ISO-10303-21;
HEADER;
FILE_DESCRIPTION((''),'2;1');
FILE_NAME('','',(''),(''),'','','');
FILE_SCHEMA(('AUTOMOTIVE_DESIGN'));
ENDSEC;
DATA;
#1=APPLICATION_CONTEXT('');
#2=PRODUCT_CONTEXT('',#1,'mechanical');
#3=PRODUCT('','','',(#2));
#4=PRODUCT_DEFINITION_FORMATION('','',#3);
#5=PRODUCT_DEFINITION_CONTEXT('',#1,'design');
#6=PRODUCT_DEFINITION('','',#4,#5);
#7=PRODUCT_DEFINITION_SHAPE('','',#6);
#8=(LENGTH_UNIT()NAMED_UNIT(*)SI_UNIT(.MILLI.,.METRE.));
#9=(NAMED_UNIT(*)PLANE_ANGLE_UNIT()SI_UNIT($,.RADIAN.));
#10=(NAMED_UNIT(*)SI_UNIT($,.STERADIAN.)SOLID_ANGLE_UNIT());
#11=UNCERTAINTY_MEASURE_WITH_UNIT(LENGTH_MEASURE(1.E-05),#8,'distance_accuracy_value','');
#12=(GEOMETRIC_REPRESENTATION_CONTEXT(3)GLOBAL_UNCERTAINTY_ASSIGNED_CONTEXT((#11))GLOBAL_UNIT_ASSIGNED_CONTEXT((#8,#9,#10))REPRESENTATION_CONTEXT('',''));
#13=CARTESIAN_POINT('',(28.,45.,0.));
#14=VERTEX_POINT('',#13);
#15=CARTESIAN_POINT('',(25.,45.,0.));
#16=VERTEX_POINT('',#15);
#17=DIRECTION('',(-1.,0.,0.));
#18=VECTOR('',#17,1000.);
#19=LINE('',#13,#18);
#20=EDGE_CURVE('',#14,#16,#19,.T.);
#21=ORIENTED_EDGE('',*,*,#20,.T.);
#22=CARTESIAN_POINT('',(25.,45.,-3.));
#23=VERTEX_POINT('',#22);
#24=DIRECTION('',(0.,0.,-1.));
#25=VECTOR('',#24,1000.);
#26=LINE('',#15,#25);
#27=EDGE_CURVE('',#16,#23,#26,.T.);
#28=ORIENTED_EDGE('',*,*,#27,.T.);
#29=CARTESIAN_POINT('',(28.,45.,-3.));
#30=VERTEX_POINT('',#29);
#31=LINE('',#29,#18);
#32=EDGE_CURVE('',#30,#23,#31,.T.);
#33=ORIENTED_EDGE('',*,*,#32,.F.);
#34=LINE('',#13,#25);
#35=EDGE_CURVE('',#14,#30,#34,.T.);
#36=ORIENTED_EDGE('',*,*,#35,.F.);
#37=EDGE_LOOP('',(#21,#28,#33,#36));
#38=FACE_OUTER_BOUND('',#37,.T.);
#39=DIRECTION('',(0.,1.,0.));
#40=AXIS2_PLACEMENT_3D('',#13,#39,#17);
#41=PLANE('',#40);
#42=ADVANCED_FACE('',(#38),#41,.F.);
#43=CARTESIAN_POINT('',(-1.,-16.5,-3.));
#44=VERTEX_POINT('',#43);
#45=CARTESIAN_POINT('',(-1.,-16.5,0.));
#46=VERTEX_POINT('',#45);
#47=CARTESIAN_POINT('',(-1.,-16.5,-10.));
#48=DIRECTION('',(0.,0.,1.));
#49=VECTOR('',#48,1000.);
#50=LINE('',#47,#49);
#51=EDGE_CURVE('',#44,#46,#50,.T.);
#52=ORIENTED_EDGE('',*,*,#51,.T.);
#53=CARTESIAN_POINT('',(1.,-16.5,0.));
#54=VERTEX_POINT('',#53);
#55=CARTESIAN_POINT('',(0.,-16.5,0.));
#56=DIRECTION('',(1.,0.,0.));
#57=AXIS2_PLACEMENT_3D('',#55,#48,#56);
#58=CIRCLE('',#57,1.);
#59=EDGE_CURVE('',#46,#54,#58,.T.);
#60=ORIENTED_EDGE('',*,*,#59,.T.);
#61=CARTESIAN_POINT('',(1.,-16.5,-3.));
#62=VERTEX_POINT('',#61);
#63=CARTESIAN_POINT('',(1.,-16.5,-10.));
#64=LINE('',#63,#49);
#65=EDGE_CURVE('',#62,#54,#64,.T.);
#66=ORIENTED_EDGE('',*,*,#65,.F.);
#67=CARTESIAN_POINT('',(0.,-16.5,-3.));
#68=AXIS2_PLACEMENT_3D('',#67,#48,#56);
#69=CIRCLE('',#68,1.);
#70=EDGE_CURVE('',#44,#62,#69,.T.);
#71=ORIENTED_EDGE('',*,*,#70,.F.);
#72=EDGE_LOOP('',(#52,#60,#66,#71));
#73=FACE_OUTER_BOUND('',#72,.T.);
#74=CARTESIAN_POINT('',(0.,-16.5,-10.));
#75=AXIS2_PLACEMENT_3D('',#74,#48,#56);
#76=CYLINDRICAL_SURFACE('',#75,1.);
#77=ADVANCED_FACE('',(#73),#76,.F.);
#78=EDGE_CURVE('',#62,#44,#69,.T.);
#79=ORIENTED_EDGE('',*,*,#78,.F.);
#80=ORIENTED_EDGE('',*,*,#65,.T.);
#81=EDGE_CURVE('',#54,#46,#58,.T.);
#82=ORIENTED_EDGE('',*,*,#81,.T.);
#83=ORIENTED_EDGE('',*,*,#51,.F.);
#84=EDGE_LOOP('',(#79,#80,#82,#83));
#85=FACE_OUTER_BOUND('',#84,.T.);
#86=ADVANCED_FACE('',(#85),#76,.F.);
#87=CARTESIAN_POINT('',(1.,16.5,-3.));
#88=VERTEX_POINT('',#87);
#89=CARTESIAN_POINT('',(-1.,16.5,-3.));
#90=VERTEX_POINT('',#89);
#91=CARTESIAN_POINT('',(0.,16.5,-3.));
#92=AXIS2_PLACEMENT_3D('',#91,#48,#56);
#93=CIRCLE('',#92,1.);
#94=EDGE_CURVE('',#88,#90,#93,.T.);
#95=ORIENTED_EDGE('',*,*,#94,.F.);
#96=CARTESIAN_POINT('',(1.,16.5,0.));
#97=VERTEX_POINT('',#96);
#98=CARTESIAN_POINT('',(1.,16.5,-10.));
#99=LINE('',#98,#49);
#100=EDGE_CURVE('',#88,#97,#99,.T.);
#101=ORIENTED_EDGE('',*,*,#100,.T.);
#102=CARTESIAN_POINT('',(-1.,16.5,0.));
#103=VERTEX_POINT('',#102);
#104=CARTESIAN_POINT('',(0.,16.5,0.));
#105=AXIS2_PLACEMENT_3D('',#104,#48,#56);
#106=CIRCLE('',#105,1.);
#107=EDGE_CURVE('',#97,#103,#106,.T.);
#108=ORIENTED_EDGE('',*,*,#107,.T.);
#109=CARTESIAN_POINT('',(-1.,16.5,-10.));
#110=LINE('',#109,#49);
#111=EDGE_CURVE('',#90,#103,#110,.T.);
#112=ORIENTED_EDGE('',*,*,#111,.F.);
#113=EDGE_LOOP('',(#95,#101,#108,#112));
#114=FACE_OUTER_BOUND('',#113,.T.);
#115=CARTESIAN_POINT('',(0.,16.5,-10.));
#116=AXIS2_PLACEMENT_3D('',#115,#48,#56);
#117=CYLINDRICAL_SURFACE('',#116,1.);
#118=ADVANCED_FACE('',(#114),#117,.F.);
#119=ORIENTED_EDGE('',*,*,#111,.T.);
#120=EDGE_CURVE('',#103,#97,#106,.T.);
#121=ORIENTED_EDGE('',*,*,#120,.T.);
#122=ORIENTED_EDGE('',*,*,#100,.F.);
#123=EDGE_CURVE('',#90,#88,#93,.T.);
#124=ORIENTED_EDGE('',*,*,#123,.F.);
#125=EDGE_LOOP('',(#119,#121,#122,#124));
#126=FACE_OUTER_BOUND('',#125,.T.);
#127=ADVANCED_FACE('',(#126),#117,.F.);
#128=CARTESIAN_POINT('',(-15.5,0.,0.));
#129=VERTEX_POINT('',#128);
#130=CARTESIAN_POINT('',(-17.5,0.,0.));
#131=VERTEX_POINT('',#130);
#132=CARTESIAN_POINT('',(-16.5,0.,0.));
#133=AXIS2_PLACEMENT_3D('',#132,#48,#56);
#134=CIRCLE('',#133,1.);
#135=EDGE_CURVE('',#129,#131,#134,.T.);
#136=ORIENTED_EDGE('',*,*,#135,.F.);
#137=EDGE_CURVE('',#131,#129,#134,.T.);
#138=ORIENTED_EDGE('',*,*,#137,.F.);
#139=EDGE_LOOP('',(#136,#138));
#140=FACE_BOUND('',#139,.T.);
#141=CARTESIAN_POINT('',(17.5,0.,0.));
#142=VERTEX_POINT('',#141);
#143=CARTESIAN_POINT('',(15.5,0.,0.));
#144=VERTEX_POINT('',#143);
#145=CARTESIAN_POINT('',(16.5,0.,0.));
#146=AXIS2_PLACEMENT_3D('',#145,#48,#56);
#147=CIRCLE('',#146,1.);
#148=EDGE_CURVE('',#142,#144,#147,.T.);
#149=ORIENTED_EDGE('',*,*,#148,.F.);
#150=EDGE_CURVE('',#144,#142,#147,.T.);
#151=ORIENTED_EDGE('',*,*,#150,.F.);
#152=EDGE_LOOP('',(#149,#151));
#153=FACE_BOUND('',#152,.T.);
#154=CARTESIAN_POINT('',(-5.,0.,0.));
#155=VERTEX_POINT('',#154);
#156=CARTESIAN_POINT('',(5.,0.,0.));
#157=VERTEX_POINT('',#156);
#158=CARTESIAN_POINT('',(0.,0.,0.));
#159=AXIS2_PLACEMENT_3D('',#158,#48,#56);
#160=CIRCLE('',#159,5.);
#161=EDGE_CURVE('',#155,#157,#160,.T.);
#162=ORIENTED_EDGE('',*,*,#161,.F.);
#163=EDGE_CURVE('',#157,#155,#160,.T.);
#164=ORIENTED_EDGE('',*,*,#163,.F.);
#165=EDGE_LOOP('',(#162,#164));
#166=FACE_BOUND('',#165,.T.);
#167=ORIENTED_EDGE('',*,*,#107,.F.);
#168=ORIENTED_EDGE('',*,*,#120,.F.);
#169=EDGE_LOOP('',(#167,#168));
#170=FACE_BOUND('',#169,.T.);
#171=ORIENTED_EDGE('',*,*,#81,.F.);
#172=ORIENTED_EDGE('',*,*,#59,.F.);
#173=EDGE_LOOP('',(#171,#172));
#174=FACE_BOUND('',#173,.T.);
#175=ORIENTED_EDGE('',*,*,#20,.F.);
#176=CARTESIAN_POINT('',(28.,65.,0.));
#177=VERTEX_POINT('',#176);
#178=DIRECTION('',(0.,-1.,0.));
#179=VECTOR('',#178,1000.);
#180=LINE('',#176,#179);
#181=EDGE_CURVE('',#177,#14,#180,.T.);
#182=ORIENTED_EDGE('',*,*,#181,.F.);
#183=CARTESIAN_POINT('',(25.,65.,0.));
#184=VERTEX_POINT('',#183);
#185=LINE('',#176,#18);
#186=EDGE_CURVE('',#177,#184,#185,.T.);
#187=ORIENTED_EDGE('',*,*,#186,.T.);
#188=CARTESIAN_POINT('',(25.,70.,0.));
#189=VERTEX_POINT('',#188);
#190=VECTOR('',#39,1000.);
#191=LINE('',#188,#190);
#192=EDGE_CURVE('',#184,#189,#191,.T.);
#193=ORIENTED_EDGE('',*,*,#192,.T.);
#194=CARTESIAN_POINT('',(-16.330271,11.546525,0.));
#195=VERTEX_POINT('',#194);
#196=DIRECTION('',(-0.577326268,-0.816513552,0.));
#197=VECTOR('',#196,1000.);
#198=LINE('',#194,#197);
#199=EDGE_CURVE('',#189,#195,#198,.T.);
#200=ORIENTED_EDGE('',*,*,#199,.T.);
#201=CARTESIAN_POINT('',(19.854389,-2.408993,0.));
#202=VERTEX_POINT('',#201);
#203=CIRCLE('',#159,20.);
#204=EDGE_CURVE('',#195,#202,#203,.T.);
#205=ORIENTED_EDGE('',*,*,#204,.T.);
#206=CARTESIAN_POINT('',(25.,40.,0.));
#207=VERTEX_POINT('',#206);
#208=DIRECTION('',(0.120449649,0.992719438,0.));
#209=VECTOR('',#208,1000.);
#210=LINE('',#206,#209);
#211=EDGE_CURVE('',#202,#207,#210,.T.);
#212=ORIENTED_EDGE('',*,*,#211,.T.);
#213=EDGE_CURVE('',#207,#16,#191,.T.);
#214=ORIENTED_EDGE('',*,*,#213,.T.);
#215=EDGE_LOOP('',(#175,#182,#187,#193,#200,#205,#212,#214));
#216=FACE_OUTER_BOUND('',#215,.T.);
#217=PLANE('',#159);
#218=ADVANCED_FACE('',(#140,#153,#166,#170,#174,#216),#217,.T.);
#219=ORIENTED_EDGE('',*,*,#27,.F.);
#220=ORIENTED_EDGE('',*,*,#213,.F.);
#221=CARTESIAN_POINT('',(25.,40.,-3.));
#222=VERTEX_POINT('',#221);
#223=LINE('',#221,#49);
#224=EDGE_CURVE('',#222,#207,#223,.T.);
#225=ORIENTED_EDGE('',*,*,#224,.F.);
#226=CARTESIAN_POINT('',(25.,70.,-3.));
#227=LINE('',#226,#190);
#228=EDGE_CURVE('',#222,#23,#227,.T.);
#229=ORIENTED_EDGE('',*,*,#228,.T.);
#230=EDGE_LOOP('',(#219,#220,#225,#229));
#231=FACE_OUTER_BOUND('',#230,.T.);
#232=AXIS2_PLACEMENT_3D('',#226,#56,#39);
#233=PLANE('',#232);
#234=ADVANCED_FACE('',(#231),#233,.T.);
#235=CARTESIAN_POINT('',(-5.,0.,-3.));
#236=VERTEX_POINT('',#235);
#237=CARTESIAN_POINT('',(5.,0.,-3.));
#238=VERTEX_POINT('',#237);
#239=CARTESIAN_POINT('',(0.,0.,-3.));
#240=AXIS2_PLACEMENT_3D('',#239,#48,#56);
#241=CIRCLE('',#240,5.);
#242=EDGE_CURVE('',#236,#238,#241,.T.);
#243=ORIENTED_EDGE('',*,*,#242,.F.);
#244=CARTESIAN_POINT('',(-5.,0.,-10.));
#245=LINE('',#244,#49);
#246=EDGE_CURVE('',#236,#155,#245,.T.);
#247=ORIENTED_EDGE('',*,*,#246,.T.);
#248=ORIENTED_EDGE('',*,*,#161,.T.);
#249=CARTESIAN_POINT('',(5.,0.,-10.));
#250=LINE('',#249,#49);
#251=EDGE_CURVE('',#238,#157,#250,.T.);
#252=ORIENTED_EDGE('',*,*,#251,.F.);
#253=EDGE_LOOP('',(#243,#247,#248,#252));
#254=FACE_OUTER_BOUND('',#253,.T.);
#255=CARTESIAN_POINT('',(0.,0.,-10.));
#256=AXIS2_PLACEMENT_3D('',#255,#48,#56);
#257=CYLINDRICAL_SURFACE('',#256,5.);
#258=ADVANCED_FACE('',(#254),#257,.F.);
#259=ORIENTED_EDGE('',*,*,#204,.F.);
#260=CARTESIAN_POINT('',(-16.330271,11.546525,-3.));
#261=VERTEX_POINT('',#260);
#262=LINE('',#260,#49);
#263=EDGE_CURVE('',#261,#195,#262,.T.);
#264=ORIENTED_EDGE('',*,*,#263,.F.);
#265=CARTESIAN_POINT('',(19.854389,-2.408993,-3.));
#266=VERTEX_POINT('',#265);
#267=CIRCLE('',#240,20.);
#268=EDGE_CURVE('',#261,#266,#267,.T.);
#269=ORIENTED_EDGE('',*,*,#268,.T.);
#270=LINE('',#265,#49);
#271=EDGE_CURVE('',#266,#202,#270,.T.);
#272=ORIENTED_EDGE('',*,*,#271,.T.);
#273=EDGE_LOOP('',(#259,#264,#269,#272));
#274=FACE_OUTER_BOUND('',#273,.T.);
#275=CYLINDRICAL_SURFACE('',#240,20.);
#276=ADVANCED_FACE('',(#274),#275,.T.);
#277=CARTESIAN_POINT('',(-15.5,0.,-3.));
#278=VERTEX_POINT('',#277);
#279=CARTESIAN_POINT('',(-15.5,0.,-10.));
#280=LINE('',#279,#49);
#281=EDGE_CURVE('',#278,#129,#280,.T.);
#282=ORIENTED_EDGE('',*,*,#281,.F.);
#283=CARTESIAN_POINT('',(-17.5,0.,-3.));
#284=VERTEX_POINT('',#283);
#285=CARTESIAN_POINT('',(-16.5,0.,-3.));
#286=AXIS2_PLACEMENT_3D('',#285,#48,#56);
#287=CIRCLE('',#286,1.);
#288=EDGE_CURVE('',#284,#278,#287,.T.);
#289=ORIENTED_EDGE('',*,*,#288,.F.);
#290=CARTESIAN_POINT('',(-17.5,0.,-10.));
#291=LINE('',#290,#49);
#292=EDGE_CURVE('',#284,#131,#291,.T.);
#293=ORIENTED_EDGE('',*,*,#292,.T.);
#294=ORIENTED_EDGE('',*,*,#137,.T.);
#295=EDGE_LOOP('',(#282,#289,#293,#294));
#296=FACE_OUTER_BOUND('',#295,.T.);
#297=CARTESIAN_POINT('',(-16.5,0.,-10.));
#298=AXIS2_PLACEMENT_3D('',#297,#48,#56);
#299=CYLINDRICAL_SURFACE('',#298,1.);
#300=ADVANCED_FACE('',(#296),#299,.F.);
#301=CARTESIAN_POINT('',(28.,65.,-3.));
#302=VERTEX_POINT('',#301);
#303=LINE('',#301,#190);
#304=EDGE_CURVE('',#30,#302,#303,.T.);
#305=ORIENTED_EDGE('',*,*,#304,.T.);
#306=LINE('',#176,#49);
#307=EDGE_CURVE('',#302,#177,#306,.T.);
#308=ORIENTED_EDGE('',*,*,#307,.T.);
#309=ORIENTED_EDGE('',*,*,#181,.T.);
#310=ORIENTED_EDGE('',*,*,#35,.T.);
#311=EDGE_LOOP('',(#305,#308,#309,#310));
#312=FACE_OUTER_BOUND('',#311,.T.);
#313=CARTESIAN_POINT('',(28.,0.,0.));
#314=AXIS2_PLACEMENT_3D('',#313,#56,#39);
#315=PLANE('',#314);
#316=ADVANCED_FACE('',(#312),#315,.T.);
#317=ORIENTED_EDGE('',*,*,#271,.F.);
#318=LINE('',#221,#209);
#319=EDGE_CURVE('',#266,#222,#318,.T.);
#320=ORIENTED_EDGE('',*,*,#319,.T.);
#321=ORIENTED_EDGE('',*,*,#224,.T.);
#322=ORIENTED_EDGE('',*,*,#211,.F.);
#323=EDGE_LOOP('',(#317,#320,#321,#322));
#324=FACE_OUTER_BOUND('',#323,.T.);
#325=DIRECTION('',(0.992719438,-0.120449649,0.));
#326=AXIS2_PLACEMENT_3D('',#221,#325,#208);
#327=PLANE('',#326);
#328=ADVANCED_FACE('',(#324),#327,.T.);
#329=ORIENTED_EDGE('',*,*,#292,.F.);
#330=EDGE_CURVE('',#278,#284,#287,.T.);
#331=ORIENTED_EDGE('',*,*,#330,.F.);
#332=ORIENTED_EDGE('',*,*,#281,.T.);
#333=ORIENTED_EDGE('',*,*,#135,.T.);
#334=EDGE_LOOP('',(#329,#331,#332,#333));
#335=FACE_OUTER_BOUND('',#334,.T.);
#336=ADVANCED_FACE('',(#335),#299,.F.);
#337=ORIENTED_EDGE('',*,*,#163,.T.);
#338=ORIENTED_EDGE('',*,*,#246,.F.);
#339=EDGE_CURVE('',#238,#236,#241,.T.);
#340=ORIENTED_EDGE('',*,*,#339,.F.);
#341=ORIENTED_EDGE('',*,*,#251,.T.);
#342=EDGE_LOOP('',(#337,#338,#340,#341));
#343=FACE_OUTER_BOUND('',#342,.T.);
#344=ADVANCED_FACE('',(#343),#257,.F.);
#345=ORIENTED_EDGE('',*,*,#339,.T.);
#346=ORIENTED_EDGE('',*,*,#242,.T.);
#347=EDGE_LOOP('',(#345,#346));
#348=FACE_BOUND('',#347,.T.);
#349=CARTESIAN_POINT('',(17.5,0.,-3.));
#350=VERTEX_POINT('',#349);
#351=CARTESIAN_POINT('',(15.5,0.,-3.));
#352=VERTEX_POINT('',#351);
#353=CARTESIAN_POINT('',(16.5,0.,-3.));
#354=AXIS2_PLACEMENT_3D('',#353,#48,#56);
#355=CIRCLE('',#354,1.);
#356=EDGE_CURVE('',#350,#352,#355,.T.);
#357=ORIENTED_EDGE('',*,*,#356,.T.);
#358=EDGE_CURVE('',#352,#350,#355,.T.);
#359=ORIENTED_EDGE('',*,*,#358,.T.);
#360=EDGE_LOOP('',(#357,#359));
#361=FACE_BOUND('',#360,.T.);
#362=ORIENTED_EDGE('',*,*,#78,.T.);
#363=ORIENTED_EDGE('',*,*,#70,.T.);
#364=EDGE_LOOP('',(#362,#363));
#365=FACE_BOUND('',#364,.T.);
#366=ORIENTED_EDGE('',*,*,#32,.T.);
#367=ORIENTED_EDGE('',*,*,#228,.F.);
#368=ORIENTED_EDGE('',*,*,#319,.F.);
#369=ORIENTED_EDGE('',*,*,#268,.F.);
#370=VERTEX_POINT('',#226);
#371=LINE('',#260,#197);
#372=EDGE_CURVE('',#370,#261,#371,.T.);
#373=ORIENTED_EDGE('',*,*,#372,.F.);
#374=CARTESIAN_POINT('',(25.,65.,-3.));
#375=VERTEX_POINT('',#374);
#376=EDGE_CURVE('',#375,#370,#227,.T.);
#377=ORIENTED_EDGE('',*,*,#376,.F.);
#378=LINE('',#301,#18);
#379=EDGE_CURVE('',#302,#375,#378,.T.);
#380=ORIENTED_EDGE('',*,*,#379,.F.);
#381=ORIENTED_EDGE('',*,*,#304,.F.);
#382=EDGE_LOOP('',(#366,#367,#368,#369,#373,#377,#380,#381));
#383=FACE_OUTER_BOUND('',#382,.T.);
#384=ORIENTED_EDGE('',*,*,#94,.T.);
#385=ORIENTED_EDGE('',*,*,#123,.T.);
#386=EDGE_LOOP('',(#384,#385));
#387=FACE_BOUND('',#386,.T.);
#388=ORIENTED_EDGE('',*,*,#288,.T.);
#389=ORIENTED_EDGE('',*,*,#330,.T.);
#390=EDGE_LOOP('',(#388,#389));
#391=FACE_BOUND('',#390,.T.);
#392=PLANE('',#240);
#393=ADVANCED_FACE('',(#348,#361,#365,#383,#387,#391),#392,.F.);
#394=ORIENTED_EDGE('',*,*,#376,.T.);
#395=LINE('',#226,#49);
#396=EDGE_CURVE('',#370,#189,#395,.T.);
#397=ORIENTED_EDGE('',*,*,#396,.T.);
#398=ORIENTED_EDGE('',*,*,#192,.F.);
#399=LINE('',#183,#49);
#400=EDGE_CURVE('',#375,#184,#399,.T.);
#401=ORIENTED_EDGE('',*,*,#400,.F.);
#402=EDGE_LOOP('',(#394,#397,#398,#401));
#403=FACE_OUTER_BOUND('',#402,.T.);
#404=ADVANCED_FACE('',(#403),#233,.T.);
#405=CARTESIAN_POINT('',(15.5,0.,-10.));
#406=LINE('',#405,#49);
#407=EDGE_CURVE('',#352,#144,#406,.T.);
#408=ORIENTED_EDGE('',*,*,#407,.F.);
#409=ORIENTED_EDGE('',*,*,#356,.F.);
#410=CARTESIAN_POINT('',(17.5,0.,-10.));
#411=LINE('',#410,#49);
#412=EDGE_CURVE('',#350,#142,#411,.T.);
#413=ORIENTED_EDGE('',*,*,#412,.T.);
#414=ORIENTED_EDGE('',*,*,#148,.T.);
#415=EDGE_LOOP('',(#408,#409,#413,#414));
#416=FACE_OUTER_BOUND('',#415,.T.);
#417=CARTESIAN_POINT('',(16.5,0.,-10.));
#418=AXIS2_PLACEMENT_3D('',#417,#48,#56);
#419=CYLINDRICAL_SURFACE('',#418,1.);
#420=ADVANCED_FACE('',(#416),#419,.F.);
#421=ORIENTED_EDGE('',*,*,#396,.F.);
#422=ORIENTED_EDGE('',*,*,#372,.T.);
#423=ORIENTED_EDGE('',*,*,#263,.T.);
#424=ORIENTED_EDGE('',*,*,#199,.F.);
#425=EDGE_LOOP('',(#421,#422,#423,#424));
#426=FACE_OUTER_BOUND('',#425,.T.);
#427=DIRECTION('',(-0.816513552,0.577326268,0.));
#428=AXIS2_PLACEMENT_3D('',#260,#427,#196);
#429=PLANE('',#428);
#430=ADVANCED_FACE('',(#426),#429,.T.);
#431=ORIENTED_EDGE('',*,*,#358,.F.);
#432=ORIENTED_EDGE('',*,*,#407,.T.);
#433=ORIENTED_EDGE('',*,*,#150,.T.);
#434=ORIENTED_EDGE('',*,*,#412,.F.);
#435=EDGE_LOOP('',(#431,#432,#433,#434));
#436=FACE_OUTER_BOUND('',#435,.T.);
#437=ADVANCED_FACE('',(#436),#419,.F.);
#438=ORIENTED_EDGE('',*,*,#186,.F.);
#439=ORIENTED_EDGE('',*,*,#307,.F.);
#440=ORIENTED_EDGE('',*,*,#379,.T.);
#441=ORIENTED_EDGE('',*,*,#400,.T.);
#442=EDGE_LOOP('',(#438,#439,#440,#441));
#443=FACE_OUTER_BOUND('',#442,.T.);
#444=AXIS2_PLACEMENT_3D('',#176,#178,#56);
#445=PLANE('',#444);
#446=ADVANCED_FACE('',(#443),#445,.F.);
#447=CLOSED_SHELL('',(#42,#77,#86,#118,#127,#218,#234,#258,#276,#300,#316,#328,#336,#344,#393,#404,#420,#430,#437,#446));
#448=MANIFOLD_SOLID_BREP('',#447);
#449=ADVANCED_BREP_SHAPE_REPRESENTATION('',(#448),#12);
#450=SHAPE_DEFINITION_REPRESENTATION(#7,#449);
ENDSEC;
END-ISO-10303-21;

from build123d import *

# Parameters (mm, degrees)
BOSS_EXTRUDE1_DEPTH = 3
SKETCH2_R           = 5
CUT_EXTRUDE1_DEPTH  = 10
SKETCH4_W           = 3
SKETCH4_H           = 20
BOSS_EXTRUDE3_DEPTH = 3
SKETCH5_R           = 1
CUT_EXTRUDE2_DEPTH  = 10


with BuildPart() as part:
    # Sketch1 → Boss-Extrude1 (new body)
    with BuildSketch(Plane.XY):
        with BuildLine():
            Line((-16.33027103, 11.546525368), (25, 70))
            Line((25, 70), (25, 40))
            Line((25, 40), (19.854388756, -2.408992972))
            ThreePointArc((19.854388756, -2.408992972), (-7.196803073, -18.660279353), (-16.33027103, 11.546525368))
        make_face()
    extrude(amount=-BOSS_EXTRUDE1_DEPTH)

    # Sketch2 → Cut-Extrude1 (cut)
    with BuildSketch(Plane.XY):
        Circle(SKETCH2_R)
    extrude(amount=-CUT_EXTRUDE1_DEPTH, mode=Mode.SUBTRACT)

    # Sketch4 → Boss-Extrude3 (add)
    with BuildSketch(Plane(origin=(25, 0, 0), x_dir=(0, 0, -1), z_dir=(1, 0, 0))):
        with Locations((1.5, 55)):
            Rectangle(SKETCH4_W, SKETCH4_H)
    extrude(amount=BOSS_EXTRUDE3_DEPTH)

    # Sketch5 → Cut-Extrude2 (cut)
    with BuildSketch(Plane.XY):
        with Locations((0, 16.5)):
            Circle(SKETCH5_R)
        with Locations((0, -16.5)):
            Circle(SKETCH5_R)
        with Locations((16.5, 0)):
            Circle(SKETCH5_R)
        with Locations((-16.5, 0)):
            Circle(SKETCH5_R)
    extrude(amount=-CUT_EXTRUDE2_DEPTH, mode=Mode.SUBTRACT)


solid = part.part
